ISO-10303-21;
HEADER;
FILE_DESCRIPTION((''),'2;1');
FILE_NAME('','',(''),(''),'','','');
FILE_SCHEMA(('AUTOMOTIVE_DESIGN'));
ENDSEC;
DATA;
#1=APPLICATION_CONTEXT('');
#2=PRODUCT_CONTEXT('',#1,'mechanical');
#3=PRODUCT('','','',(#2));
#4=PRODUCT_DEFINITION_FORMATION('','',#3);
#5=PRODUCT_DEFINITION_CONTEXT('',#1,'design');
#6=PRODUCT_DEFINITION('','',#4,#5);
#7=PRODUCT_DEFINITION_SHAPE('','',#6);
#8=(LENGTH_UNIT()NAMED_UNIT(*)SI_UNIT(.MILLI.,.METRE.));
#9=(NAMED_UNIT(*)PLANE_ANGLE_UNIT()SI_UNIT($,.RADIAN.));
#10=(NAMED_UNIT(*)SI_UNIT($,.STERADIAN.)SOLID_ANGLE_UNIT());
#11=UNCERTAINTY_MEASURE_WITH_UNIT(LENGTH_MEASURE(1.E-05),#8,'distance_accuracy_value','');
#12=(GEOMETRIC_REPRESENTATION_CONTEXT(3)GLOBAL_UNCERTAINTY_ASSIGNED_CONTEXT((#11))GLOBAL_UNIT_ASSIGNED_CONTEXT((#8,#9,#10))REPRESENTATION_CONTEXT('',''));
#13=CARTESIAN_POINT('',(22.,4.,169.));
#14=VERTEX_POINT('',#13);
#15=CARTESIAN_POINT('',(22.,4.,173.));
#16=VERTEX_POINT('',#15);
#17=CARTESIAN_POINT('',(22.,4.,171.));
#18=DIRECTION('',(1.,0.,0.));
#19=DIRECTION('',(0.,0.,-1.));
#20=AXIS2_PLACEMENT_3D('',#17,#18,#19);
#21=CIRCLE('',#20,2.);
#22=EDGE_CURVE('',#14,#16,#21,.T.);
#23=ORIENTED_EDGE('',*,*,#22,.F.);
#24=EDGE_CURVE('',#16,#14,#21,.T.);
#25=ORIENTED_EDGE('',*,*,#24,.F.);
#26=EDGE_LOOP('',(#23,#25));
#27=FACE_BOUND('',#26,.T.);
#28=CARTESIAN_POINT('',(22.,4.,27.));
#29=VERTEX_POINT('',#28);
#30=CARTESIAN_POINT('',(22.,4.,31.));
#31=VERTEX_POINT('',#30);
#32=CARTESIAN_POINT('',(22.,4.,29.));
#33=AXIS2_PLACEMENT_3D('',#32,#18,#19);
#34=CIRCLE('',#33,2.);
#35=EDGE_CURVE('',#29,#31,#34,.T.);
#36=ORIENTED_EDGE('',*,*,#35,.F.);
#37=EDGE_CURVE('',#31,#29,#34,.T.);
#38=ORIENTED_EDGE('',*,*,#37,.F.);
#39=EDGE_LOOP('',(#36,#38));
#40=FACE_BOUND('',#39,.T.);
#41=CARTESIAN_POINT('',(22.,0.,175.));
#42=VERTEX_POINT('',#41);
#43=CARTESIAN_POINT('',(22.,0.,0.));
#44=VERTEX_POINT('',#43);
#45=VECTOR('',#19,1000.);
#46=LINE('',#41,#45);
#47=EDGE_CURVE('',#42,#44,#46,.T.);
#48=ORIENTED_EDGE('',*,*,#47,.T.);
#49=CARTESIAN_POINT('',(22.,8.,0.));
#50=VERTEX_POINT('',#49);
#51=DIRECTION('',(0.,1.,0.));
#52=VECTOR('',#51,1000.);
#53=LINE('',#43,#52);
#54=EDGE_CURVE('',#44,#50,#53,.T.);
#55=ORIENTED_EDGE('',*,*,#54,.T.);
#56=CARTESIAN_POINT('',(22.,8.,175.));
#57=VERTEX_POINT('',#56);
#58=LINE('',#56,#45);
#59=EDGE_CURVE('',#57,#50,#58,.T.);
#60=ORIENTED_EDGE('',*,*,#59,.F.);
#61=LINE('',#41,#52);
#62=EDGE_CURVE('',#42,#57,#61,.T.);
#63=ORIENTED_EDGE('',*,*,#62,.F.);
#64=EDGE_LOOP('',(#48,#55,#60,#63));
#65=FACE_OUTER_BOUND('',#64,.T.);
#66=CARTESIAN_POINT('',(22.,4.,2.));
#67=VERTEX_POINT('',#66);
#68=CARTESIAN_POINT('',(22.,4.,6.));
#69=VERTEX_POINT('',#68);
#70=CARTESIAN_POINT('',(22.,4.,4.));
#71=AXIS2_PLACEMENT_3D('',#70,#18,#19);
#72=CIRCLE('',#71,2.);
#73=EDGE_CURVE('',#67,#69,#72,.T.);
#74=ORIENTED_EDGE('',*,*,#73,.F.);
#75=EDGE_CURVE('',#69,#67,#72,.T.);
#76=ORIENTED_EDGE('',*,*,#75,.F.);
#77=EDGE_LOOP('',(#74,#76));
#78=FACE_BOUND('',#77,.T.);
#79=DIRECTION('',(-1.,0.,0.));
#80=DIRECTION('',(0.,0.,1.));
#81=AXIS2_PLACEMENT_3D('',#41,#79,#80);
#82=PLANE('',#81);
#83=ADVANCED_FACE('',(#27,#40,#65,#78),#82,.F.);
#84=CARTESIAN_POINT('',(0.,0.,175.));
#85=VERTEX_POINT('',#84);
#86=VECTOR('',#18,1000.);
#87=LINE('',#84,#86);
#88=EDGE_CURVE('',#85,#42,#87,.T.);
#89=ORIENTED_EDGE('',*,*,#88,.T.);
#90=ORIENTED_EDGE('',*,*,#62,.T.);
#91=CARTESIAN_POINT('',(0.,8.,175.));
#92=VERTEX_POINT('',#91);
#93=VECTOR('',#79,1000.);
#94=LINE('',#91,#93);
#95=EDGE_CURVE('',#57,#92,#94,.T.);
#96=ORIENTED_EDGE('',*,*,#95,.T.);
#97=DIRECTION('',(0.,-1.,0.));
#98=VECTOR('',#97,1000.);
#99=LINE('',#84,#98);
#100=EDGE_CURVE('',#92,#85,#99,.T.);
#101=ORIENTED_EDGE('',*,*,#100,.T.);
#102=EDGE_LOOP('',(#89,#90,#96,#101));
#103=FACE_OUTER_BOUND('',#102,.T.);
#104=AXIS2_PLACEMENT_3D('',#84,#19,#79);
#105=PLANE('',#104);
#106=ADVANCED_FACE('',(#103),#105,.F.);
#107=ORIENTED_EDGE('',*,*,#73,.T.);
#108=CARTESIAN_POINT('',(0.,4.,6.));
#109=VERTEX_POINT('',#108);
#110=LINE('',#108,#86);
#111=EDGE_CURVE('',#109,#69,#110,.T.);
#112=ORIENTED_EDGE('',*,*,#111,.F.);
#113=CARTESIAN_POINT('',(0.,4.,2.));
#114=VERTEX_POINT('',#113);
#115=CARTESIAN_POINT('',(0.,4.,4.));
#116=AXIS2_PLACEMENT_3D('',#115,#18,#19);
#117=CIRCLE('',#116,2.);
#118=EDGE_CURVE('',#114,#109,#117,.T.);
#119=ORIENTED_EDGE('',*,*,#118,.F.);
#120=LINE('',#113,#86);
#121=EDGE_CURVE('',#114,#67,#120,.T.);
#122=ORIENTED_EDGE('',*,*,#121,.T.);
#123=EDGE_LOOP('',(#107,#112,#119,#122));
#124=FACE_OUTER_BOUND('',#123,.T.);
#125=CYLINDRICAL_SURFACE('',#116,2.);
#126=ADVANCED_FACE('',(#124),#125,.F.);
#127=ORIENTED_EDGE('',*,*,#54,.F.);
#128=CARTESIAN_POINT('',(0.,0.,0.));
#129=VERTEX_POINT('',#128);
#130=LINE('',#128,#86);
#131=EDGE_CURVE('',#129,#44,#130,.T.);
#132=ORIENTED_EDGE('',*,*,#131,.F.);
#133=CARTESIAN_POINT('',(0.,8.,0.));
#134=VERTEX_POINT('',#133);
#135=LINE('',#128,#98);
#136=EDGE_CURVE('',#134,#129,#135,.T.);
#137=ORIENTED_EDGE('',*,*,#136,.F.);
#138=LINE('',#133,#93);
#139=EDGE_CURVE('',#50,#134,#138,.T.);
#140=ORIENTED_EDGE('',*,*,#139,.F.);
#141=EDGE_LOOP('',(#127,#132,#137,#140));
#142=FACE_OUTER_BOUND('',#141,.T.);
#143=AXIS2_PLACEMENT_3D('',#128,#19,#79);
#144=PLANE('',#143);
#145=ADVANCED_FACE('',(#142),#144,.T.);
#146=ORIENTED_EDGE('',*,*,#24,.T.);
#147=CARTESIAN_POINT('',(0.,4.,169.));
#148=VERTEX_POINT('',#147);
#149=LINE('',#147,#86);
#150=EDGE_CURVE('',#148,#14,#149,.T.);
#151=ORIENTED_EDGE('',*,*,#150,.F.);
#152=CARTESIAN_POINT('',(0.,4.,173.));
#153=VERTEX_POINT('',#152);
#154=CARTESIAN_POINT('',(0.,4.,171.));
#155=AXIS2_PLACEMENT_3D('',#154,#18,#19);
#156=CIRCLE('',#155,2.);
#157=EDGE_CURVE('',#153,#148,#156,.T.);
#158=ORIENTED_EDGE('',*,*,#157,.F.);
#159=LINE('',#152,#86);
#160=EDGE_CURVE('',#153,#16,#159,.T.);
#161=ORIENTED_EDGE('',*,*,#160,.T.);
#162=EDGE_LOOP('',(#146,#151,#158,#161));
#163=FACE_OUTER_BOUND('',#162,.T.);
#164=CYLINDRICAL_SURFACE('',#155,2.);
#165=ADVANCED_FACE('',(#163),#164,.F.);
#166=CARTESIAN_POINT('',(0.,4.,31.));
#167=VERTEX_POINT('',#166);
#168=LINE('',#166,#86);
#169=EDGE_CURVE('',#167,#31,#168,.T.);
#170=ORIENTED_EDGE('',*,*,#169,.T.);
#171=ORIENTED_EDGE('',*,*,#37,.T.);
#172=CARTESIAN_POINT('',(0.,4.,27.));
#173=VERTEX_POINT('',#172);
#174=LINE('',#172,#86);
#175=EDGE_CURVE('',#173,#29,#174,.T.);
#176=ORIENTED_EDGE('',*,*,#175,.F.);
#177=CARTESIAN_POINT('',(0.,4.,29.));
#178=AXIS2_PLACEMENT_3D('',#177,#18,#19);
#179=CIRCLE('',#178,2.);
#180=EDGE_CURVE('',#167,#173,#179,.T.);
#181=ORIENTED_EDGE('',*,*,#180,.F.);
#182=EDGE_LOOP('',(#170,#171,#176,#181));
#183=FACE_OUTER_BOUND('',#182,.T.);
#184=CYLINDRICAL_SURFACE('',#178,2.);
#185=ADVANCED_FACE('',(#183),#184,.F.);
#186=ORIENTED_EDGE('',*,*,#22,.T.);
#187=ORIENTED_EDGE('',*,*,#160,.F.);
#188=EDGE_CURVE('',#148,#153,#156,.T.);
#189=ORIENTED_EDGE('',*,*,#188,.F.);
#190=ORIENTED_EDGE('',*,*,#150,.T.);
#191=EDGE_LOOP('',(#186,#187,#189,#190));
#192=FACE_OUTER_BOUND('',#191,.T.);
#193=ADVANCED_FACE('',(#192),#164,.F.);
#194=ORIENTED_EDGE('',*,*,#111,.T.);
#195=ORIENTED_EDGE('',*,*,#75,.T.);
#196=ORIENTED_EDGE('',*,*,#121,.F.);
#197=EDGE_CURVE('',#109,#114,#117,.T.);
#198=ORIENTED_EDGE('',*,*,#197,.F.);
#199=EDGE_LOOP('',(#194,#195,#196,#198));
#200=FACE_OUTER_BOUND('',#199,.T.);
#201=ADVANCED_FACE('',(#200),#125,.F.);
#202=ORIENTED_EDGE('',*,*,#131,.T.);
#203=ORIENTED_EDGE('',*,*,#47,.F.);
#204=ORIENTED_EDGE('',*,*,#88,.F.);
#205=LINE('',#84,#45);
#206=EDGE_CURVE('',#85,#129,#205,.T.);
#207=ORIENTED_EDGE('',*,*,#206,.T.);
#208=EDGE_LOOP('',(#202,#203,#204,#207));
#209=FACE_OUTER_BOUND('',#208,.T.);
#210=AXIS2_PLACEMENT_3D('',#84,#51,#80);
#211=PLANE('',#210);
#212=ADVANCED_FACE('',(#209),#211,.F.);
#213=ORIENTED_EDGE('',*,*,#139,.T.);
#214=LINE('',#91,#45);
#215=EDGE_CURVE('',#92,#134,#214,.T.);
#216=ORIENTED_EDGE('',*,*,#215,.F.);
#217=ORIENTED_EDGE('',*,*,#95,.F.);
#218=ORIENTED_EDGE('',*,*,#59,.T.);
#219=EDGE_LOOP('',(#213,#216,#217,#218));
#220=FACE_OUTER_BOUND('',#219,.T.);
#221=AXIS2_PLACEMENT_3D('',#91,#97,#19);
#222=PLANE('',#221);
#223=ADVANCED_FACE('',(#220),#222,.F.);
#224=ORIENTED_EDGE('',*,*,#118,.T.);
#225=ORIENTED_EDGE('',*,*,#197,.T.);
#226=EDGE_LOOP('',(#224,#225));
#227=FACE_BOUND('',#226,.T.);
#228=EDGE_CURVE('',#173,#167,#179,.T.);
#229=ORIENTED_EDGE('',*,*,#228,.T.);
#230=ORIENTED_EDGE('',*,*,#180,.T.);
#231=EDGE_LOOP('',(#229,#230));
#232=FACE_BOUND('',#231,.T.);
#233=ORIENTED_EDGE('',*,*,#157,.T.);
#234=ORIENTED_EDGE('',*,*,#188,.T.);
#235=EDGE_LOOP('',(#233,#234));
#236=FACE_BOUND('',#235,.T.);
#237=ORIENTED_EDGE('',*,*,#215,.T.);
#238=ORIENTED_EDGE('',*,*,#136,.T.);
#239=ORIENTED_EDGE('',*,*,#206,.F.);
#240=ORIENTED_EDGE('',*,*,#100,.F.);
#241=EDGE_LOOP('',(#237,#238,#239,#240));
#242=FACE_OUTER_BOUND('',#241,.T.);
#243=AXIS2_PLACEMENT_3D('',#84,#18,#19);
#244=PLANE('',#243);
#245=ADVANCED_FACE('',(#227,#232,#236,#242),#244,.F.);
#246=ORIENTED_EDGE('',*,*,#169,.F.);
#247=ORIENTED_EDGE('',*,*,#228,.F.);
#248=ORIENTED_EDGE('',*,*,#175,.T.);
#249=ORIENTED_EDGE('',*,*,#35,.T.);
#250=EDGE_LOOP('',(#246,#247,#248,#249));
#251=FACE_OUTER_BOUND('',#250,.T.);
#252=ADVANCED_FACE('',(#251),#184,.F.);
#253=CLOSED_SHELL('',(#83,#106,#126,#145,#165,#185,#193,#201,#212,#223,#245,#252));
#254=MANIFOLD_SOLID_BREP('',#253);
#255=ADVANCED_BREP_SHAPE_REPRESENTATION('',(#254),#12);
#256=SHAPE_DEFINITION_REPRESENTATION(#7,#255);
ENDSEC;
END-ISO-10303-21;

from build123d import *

# Parameters (mm, degrees)
SKETCH1_W           = 22
SKETCH1_H           = 8
BOSS_EXTRUDE1_DEPTH = 175
SKETCH2_R           = 2
CUT_EXTRUDE1_DEPTH  = 177.558772085


with BuildPart() as part:
    # Sketch1 → Boss-Extrude1 (new body)
    with BuildSketch(Plane.XY):
        with Locations((11, 4)):
            Rectangle(SKETCH1_W, SKETCH1_H)
    extrude(amount=BOSS_EXTRUDE1_DEPTH)

    # Sketch2 → Cut-Extrude1 (cut, through all)
    with BuildSketch(Plane(origin=(22, 0, 0), x_dir=(0, 0, -1), z_dir=(1, 0, 0))):
        with Locations((-4, 4)):
            Circle(SKETCH2_R)
        with Locations((-171, 4)):
            Circle(SKETCH2_R)
        with Locations((-29, 4)):
            Circle(SKETCH2_R)
    extrude(amount=-CUT_EXTRUDE1_DEPTH, mode=Mode.SUBTRACT)


solid = part.part
